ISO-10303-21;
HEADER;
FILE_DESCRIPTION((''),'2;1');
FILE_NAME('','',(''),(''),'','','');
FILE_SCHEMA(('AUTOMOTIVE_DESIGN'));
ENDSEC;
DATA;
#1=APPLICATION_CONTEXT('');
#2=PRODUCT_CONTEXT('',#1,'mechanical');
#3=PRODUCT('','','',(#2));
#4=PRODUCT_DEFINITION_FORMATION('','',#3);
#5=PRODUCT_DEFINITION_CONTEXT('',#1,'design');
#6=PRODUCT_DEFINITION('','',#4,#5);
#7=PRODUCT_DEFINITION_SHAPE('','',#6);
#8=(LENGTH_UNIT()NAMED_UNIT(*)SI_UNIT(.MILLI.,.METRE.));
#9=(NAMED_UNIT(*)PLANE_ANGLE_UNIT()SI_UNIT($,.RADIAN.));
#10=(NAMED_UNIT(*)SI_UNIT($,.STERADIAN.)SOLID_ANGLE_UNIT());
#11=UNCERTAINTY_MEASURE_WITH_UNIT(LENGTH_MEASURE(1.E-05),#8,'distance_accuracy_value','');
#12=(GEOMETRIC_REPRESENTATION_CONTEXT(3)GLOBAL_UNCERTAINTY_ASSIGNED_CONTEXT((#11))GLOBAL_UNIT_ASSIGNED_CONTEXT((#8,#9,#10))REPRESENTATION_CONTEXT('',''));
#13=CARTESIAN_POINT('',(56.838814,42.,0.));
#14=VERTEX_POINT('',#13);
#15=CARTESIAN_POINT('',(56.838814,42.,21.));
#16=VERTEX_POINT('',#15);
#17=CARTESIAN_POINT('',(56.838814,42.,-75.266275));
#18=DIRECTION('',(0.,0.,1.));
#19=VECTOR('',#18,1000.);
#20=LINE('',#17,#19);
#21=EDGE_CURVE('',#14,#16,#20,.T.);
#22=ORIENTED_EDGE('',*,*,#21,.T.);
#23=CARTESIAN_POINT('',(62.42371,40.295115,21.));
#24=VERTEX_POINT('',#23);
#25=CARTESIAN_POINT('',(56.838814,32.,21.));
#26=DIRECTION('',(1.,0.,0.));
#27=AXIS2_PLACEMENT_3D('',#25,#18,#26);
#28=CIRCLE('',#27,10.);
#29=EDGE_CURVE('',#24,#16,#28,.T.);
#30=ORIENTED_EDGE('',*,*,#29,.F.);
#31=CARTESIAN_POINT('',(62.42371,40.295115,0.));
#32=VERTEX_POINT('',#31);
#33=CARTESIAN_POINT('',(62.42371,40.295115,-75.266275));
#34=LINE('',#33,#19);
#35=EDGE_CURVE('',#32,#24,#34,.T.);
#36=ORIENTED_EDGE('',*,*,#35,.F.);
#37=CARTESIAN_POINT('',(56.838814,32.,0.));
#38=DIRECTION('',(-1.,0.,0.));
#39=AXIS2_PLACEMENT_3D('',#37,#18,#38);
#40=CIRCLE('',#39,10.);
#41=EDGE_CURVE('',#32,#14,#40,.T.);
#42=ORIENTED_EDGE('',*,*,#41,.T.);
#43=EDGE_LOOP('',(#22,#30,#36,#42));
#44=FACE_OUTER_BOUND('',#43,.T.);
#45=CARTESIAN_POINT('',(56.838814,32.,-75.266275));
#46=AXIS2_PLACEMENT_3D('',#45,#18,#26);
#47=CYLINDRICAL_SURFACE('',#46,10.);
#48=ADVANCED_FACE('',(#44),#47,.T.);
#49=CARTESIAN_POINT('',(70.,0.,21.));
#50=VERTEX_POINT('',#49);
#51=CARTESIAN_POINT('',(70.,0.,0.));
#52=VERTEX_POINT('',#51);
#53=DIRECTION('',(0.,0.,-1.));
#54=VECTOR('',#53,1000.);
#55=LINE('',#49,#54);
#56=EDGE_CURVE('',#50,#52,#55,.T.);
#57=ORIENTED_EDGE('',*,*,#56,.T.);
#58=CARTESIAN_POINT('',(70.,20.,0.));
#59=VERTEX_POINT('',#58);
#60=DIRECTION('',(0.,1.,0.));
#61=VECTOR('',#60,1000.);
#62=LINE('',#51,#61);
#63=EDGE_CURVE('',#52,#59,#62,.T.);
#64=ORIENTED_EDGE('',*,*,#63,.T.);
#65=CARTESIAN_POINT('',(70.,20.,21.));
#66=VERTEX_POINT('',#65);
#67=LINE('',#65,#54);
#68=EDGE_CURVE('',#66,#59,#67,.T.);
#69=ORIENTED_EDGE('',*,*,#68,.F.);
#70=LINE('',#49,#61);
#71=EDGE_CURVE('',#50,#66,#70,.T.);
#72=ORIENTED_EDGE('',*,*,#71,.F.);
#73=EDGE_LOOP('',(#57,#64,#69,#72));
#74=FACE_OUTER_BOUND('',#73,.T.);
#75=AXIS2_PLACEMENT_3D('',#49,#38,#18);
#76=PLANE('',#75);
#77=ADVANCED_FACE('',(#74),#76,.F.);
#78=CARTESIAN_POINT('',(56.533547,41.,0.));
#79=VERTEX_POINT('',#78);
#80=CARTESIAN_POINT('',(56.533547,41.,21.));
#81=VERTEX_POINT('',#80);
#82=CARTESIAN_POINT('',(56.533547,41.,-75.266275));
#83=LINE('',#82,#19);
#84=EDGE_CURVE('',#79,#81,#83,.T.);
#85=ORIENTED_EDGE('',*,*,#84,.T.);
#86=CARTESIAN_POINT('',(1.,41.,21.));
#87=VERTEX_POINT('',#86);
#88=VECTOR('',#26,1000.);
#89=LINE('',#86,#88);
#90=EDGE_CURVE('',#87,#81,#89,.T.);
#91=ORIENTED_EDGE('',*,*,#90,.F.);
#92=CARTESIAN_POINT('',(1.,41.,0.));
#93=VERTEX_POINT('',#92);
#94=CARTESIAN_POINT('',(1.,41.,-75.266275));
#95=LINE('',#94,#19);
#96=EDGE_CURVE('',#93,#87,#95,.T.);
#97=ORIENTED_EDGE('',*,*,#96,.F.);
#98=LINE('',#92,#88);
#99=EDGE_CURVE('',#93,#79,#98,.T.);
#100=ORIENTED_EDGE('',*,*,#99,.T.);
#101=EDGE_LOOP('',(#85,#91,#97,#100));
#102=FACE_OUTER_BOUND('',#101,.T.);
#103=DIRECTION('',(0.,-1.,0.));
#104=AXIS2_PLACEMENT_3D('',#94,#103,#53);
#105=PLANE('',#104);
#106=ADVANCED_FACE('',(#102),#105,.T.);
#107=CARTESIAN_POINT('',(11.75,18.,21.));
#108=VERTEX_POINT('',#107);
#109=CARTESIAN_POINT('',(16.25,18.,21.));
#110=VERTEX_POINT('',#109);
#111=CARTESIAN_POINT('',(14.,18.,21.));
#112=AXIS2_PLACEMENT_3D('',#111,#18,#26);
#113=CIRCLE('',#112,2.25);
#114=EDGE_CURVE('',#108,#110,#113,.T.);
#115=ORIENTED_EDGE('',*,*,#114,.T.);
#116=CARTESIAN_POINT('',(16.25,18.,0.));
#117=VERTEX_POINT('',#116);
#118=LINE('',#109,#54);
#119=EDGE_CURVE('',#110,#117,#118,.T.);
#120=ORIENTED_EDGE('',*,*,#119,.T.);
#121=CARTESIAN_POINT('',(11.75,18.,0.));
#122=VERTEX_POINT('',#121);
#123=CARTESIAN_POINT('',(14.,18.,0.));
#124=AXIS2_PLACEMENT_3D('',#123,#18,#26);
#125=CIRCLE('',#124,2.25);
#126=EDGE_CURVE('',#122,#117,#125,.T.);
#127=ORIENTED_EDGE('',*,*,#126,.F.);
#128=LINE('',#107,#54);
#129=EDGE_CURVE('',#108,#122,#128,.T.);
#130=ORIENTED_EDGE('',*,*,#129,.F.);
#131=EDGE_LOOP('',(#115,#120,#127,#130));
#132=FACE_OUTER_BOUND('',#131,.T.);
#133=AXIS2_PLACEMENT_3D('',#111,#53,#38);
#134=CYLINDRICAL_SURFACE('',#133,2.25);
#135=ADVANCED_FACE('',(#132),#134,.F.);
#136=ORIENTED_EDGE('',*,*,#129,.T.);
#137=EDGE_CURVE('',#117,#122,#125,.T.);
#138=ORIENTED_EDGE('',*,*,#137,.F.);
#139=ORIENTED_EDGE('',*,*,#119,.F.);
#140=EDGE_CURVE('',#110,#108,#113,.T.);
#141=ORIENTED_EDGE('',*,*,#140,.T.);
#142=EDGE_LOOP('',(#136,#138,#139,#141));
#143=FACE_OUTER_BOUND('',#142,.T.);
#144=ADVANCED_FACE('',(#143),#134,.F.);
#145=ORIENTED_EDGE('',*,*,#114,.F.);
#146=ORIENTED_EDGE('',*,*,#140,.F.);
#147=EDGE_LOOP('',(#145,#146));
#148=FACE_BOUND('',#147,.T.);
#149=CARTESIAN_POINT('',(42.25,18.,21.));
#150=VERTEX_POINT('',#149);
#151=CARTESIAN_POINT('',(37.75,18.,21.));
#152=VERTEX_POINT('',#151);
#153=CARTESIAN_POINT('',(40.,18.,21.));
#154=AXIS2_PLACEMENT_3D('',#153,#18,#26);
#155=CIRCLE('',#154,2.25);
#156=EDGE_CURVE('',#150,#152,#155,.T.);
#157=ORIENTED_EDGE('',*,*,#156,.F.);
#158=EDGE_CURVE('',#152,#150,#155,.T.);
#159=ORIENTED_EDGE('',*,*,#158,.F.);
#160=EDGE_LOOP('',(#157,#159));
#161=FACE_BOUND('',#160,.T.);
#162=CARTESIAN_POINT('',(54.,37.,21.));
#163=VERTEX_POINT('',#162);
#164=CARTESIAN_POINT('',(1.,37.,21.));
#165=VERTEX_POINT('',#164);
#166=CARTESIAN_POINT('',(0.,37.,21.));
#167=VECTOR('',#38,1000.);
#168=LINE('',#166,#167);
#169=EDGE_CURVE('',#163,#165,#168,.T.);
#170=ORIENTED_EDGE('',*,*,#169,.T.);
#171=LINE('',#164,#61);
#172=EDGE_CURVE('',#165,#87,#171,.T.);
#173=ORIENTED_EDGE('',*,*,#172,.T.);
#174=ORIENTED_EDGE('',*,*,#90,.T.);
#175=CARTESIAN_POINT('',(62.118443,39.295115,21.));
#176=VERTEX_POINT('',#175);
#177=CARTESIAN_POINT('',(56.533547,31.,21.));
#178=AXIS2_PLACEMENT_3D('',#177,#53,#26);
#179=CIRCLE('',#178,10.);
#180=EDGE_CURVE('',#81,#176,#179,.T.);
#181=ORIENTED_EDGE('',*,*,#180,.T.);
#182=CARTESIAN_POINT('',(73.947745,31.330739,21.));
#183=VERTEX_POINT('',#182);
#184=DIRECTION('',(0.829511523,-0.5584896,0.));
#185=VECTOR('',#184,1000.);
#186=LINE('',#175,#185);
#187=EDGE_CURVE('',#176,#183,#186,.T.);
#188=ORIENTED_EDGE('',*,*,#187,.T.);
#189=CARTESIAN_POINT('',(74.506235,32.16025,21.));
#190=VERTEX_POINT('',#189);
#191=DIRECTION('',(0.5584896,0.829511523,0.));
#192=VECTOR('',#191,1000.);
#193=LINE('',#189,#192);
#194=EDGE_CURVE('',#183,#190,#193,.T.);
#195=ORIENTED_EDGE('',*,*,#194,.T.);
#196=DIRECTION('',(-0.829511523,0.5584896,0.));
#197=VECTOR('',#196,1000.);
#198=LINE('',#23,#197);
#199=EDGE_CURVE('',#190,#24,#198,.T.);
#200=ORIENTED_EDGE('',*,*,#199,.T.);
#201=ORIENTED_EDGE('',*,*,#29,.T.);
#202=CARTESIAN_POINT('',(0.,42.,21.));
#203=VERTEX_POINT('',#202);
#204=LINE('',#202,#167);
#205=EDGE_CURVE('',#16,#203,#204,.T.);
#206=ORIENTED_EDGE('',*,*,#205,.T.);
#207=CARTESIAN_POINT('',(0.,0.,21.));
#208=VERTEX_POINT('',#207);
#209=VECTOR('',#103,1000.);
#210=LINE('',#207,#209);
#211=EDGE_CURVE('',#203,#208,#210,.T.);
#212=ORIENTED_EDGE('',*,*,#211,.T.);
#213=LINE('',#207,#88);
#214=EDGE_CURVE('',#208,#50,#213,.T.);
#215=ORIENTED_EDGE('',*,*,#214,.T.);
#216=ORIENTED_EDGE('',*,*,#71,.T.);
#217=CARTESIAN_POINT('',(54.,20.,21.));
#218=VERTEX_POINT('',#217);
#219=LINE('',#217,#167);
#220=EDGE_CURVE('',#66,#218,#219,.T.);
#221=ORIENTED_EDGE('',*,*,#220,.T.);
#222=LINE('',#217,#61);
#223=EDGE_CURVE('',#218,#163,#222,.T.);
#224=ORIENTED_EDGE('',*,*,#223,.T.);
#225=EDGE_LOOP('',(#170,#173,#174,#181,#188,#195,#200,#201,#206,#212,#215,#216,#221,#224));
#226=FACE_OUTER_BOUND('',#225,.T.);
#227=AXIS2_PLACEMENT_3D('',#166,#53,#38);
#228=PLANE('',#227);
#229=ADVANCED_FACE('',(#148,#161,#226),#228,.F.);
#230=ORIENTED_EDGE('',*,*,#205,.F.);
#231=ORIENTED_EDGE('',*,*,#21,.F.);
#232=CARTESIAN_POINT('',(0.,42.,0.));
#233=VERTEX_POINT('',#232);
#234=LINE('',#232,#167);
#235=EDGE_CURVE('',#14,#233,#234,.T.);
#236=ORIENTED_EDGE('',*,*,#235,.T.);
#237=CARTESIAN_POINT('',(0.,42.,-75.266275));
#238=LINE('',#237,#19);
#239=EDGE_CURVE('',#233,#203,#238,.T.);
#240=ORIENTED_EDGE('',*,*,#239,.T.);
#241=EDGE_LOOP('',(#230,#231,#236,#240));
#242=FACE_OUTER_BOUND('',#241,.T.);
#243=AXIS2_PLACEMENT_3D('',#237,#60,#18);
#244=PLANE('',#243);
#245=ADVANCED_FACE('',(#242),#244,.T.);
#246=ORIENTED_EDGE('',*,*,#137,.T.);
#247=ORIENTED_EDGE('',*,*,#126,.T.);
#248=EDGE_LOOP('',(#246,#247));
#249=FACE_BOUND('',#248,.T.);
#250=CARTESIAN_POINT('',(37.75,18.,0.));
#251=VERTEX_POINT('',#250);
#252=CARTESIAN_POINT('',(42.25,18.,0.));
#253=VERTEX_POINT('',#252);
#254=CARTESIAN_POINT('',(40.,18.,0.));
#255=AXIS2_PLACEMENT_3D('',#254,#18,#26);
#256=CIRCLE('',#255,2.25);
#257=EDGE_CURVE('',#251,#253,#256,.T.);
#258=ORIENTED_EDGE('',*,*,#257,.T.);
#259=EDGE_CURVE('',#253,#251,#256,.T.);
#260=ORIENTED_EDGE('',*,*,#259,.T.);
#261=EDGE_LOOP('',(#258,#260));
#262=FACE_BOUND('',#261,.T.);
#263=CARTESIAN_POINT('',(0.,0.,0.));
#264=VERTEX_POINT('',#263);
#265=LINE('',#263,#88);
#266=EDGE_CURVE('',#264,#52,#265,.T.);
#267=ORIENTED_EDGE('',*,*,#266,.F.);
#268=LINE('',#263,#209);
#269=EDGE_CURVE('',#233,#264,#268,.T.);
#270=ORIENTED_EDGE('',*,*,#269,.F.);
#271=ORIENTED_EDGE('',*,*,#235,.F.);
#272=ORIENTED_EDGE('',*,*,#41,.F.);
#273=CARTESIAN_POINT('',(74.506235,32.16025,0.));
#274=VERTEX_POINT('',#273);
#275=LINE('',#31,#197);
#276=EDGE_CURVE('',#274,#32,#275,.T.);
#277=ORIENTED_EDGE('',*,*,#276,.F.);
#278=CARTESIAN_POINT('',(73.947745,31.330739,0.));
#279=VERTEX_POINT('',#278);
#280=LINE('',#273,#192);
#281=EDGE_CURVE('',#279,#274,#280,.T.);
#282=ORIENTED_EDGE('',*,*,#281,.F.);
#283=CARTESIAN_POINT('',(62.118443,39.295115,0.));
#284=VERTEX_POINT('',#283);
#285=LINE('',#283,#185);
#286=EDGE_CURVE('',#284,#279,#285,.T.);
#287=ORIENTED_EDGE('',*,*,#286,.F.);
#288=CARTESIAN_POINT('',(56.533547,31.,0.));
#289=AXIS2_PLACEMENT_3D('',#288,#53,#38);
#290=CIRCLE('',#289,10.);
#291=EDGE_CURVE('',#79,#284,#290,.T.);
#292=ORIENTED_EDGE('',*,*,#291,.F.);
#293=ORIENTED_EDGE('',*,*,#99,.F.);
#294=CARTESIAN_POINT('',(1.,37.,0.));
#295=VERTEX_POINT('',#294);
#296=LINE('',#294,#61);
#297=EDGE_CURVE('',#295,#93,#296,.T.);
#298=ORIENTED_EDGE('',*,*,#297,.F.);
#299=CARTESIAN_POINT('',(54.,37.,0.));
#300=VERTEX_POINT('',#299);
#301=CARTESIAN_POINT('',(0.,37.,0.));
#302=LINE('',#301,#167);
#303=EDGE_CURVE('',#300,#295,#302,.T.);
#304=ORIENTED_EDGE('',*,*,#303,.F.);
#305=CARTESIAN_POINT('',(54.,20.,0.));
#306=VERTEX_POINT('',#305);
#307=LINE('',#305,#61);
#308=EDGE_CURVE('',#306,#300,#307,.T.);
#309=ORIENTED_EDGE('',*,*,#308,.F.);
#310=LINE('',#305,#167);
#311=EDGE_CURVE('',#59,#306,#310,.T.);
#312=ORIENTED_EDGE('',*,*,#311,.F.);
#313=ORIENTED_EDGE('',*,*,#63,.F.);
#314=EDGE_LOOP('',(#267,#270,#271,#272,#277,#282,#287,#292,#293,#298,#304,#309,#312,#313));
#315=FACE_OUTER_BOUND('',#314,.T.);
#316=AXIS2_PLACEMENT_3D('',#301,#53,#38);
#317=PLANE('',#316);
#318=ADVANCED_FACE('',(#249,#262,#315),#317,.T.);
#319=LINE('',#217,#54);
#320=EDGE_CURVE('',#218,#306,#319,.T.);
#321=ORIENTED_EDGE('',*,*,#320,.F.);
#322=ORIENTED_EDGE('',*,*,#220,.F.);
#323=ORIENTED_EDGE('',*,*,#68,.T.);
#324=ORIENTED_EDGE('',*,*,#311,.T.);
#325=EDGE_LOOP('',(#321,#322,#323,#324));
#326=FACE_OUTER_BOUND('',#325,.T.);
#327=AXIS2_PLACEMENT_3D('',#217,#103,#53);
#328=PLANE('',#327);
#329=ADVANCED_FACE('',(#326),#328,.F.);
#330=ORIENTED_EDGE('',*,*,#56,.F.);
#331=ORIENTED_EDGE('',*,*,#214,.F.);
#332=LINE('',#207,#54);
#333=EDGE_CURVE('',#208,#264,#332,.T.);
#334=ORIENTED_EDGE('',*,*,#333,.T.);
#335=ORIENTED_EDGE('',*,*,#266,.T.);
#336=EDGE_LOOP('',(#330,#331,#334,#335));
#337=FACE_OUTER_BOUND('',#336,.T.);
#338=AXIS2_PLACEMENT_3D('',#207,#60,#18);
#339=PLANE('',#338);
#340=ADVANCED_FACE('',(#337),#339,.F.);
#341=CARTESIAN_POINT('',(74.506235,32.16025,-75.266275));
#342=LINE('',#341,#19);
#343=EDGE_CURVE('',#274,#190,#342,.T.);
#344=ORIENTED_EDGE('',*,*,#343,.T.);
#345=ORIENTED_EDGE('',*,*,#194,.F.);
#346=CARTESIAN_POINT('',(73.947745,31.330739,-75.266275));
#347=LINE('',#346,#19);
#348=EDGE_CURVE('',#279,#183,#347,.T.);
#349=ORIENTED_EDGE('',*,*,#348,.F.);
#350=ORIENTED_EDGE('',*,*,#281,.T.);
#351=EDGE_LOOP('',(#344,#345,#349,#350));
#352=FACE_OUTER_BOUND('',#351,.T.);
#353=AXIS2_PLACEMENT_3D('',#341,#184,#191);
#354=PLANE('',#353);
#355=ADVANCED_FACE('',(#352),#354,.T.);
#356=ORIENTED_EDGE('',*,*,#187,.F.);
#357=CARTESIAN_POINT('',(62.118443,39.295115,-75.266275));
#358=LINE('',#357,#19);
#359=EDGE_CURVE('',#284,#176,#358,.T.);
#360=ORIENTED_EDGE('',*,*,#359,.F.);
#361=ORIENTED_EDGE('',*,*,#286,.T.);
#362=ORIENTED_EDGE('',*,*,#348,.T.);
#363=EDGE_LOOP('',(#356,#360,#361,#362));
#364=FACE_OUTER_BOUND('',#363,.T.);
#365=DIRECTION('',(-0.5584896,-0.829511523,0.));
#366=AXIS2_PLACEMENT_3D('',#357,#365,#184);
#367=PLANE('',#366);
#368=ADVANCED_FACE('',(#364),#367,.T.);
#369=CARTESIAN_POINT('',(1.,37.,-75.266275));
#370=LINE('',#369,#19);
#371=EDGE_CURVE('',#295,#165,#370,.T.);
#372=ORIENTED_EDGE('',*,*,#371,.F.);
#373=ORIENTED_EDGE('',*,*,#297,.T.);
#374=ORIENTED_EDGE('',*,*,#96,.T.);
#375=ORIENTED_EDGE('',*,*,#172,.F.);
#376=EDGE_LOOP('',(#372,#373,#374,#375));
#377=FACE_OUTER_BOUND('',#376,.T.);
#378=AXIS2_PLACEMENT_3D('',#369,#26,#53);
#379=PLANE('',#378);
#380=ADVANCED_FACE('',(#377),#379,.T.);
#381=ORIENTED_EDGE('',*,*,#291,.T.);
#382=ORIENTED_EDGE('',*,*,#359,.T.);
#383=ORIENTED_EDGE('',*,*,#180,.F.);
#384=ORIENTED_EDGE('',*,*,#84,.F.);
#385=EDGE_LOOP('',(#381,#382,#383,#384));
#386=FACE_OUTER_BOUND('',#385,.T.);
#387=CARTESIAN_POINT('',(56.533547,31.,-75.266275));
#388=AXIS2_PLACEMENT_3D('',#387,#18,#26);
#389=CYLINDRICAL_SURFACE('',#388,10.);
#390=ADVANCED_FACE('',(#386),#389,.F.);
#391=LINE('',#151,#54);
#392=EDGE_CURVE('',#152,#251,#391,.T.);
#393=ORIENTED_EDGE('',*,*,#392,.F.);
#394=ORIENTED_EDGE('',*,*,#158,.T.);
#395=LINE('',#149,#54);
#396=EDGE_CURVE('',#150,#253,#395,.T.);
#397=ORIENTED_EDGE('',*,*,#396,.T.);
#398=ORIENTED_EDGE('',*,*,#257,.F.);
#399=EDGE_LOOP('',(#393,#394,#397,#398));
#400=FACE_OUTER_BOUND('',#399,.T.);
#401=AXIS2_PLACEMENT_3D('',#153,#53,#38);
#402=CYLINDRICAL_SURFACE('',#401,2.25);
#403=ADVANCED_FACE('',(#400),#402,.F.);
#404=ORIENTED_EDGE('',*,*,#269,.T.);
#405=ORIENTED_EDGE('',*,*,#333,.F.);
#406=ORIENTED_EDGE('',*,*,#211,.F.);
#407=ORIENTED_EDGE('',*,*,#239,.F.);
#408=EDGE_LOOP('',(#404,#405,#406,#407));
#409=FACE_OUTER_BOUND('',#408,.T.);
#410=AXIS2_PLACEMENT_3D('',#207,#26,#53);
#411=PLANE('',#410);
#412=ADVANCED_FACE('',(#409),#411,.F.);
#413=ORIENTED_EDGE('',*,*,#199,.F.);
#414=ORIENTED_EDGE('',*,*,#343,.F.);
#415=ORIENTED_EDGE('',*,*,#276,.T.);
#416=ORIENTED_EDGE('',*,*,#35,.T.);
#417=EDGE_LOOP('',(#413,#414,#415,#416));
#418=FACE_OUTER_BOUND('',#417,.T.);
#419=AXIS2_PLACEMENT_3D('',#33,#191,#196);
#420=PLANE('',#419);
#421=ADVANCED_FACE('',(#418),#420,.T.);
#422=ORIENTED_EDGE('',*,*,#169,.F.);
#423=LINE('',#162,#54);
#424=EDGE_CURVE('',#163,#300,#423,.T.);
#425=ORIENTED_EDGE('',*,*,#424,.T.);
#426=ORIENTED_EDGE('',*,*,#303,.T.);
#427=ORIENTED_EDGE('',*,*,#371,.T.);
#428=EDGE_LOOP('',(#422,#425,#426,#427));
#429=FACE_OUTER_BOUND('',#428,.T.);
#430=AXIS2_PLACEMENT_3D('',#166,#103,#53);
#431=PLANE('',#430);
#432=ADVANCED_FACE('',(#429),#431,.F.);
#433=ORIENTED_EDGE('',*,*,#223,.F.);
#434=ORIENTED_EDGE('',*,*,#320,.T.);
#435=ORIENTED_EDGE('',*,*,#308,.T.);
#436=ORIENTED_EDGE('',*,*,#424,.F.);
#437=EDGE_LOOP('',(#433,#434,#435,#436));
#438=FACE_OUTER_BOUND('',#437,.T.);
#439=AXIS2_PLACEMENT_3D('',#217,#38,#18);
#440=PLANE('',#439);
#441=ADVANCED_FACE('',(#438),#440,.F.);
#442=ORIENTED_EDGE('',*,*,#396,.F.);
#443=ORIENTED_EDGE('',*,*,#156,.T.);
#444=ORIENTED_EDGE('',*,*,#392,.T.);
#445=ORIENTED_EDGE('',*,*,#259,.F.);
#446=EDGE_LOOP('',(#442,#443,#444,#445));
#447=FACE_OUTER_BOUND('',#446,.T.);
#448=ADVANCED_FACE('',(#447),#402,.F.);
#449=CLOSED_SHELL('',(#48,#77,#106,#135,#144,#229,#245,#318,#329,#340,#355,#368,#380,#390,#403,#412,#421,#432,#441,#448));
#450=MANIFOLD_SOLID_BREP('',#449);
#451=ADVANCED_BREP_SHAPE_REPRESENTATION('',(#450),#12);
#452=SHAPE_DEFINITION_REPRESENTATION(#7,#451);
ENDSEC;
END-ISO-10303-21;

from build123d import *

# Parameters (mm, degrees)
SKETCH_1_R      = 2.25
EXTRUDE_1_DEPTH = 21
EXTRUDE_3_DEPTH = 21


with BuildPart() as part:
    # 草图1 → 凸台-拉伸1 (new body)
    with BuildSketch(Plane.XY):
        Polygon((0, 0), (70, 0), (70, 20), (54, 20), (54, 37), (0, 37), align=None)
        with Locations(Location((14, 18, 0), (0, 0, 180))):
            Circle(SKETCH_1_R, mode=Mode.SUBTRACT)
        with Locations(Location((40, 18, 0), (0, 0, 180))):
            Circle(SKETCH_1_R, mode=Mode.SUBTRACT)
    extrude(amount=EXTRUDE_1_DEPTH)

    # 草图2 → 凸台-拉伸3 (add)
    with BuildSketch(Plane.XY.offset(21)):
        with BuildLine():
            Line((62.423710356, 40.295115228), (74.506235043, 32.160250075))
            Line((74.506235043, 32.160250075), (73.947745443, 31.330738552))
            Line((73.947745443, 31.330738552), (62.118443298, 39.295115228))
            ThreePointArc((62.118443298, 39.295115228), (59.453208897, 40.564286494), (56.533547297, 41))
            Line((56.533547297, 41), (1, 41))
            Line((1, 41), (1, 37))
            Line((1, 37), (0, 37))
            Line((0, 37), (0, 42))
            Line((0, 42), (56.838814355, 42))
            ThreePointArc((56.838814355, 42), (59.758475955, 41.564286494), (62.423710356, 40.295115228))
        make_face()
    extrude(amount=-EXTRUDE_3_DEPTH)


solid = part.part
